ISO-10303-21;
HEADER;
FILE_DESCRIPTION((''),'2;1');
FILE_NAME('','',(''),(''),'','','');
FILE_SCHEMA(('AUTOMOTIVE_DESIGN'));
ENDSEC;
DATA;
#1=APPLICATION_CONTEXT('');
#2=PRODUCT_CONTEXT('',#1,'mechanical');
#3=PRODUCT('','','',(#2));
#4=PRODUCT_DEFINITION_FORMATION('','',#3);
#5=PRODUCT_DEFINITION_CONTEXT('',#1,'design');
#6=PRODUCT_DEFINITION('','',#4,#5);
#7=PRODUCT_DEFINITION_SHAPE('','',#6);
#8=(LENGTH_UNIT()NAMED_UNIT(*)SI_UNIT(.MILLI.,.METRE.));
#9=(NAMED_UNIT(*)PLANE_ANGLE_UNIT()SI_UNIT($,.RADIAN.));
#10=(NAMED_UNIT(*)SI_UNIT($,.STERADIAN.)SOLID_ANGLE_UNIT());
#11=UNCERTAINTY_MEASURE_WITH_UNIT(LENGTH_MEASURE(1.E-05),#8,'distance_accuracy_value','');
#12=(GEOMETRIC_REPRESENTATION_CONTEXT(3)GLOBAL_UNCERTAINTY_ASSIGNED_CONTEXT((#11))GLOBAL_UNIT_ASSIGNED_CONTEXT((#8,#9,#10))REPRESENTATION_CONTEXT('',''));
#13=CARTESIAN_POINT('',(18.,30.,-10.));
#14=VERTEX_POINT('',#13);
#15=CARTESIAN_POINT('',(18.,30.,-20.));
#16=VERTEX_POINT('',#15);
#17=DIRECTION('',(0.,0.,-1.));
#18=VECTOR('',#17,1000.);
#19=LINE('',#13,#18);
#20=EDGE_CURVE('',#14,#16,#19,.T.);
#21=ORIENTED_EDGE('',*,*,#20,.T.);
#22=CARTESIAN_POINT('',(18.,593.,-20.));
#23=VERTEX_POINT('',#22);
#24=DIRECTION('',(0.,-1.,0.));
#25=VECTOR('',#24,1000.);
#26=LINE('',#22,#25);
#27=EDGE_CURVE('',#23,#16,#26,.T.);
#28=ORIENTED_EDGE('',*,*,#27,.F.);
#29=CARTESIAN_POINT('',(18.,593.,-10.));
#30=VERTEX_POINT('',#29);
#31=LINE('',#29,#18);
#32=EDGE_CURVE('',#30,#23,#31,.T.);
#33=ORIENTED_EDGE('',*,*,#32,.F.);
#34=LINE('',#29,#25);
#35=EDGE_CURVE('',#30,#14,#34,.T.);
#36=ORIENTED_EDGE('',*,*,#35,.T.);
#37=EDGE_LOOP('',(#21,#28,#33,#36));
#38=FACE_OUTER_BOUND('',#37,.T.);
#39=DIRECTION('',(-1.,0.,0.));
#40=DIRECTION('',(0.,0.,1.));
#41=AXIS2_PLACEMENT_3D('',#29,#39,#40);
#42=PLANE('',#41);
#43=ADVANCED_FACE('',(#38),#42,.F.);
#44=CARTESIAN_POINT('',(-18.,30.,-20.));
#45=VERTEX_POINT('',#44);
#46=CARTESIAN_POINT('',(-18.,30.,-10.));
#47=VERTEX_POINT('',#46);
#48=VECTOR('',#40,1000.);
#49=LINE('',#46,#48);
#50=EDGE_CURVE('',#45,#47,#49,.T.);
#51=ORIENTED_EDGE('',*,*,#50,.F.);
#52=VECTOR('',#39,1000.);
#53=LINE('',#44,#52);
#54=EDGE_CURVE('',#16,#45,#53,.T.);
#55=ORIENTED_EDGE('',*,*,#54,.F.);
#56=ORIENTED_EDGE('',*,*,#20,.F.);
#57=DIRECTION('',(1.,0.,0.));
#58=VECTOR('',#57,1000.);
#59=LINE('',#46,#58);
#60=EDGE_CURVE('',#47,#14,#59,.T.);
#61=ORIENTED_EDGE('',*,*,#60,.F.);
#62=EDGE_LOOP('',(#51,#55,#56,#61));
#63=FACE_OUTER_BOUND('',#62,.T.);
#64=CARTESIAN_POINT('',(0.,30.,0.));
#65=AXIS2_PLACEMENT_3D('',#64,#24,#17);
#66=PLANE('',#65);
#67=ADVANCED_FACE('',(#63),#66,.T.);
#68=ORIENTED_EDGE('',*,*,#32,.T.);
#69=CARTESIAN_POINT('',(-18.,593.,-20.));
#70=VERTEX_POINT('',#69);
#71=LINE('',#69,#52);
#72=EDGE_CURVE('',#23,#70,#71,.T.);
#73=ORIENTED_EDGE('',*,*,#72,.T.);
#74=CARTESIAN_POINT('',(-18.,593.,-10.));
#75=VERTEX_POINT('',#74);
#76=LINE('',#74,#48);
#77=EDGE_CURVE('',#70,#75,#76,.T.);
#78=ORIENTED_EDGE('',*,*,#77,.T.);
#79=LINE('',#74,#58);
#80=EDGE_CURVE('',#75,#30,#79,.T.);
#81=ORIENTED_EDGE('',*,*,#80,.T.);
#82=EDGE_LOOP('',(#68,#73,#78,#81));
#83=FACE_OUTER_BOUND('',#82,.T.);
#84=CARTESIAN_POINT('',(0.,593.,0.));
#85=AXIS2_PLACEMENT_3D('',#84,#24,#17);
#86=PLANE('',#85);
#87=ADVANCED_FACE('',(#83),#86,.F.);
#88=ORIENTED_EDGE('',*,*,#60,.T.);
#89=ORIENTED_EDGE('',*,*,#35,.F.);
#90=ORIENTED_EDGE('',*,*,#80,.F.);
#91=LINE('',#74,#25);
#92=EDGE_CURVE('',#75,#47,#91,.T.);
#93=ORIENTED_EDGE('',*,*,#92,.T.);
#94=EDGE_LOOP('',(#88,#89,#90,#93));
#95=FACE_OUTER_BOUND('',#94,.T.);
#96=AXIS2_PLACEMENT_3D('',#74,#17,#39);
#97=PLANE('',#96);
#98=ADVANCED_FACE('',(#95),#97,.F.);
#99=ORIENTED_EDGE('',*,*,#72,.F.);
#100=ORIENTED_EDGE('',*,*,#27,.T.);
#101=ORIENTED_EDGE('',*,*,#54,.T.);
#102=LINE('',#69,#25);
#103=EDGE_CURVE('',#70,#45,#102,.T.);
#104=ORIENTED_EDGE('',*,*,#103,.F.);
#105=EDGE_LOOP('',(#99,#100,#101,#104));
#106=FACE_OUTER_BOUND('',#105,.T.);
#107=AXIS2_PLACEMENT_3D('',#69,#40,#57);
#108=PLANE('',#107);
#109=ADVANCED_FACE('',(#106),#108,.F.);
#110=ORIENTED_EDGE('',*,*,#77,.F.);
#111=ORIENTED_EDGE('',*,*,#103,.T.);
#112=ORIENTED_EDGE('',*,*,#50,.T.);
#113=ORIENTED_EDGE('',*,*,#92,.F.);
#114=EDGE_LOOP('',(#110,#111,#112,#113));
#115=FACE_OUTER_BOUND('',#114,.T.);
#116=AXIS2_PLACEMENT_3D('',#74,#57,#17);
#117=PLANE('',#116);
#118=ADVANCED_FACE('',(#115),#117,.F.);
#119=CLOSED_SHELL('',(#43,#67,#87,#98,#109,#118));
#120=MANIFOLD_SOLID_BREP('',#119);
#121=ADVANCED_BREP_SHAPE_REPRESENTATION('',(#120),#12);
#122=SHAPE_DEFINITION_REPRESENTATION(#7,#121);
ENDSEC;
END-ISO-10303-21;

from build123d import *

# Parameters (mm, degrees)
SKETCH_1_W      = 36
SKETCH_1_H      = 10
EXTRUDE_1_DEPTH = 563


with BuildPart() as part:
    # 草图1 → 凸台-拉伸1 (new body)
    with BuildSketch(Plane(origin=(0, 30, 0), x_dir=(1, 0, 0), z_dir=(0, 1, 0))):
        with Locations((0, 15)):
            Rectangle(SKETCH_1_W, SKETCH_1_H)
    extrude(amount=EXTRUDE_1_DEPTH)


solid = part.part
